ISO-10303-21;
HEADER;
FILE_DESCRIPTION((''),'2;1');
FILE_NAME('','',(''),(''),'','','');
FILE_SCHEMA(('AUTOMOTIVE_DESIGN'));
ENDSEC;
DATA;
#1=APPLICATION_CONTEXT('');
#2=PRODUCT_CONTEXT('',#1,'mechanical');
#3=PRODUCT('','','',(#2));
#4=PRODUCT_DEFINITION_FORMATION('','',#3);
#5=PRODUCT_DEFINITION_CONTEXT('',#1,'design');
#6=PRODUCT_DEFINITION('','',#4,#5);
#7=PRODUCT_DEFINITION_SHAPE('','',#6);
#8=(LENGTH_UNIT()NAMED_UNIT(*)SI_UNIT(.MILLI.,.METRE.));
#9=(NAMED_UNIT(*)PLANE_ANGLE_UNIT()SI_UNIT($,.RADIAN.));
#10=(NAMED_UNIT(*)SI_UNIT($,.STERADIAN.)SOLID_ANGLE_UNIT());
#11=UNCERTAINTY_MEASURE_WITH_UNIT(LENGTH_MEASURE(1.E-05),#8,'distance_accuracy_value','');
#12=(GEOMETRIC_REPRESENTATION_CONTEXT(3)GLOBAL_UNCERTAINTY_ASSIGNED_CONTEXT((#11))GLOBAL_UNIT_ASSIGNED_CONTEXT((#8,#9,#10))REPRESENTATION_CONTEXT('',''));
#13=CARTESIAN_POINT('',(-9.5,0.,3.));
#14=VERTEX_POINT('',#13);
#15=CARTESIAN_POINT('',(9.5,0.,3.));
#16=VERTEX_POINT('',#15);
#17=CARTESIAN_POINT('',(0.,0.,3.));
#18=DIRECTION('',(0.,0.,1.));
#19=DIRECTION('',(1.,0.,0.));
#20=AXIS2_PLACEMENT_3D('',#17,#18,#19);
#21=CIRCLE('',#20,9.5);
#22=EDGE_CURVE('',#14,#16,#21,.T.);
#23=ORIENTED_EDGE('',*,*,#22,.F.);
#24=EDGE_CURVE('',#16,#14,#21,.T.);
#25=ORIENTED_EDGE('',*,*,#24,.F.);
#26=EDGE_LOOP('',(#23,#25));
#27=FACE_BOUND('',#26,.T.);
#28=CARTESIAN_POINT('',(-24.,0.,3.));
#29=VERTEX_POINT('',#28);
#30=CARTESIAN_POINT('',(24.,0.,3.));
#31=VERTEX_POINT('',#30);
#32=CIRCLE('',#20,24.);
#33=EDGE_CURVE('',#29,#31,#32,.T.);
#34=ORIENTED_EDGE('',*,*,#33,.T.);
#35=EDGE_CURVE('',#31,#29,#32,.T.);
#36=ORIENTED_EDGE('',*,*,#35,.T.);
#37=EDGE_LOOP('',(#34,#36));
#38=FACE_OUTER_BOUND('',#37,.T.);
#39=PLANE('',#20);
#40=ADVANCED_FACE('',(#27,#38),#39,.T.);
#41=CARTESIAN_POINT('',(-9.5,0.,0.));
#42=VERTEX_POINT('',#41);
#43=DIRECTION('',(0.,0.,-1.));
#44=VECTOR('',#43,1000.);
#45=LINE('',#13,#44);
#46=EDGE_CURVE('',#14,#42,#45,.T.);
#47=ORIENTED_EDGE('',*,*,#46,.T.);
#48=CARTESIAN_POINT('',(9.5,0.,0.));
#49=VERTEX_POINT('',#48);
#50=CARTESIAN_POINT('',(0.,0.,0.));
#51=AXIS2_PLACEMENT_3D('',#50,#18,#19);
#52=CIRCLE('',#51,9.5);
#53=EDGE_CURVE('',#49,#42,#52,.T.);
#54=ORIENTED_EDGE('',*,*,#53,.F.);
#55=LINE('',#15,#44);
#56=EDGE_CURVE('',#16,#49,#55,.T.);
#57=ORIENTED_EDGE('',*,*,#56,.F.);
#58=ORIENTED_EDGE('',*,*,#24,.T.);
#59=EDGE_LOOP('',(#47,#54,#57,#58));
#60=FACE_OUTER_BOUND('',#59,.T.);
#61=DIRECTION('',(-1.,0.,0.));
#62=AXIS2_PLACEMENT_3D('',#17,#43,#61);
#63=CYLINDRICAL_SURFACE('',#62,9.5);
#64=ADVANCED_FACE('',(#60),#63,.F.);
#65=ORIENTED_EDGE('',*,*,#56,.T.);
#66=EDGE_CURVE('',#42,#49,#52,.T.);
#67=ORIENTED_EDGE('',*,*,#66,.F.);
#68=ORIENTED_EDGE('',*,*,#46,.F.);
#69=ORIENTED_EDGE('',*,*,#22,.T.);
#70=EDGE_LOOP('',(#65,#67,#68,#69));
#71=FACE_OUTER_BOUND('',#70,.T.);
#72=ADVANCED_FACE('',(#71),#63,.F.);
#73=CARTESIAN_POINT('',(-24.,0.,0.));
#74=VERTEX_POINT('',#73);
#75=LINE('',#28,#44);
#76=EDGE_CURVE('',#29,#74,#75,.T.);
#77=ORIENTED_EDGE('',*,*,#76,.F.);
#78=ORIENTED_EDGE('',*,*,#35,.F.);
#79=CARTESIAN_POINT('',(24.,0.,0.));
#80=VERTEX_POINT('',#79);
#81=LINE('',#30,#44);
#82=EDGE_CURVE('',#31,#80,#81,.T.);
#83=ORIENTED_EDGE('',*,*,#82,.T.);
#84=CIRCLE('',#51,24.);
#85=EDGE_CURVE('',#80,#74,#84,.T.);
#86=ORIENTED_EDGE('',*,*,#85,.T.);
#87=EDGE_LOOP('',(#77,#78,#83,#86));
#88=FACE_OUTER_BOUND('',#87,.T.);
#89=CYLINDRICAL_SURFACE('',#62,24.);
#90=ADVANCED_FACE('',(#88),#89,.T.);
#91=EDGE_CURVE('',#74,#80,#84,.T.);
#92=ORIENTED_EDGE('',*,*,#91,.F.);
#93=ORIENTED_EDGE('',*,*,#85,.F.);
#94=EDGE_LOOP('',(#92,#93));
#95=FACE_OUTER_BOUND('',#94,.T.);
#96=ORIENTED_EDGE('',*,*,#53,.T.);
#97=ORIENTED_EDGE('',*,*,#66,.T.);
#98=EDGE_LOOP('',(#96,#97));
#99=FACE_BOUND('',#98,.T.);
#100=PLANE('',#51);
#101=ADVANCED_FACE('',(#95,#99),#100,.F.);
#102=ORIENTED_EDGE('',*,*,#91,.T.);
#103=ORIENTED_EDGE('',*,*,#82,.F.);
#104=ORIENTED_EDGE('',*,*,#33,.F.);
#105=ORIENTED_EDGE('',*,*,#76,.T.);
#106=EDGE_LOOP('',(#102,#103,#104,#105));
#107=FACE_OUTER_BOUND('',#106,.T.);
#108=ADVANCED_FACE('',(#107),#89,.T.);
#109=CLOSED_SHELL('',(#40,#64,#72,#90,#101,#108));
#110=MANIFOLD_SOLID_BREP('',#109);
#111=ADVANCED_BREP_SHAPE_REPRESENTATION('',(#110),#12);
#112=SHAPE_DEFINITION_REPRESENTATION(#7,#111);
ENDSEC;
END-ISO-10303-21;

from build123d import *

# Parameters (mm, degrees)
SKETCH1_R      = 24
SKETCH1_R_2    = 9.5
EXTRUDE1_DEPTH = 3


with BuildPart() as part:
    # Sketch1 → Extrude1 (new body)
    with BuildSketch(Plane.XY):
        Circle(SKETCH1_R)
        Circle(SKETCH1_R_2, mode=Mode.SUBTRACT)
    extrude(amount=EXTRUDE1_DEPTH)


solid = part.part
